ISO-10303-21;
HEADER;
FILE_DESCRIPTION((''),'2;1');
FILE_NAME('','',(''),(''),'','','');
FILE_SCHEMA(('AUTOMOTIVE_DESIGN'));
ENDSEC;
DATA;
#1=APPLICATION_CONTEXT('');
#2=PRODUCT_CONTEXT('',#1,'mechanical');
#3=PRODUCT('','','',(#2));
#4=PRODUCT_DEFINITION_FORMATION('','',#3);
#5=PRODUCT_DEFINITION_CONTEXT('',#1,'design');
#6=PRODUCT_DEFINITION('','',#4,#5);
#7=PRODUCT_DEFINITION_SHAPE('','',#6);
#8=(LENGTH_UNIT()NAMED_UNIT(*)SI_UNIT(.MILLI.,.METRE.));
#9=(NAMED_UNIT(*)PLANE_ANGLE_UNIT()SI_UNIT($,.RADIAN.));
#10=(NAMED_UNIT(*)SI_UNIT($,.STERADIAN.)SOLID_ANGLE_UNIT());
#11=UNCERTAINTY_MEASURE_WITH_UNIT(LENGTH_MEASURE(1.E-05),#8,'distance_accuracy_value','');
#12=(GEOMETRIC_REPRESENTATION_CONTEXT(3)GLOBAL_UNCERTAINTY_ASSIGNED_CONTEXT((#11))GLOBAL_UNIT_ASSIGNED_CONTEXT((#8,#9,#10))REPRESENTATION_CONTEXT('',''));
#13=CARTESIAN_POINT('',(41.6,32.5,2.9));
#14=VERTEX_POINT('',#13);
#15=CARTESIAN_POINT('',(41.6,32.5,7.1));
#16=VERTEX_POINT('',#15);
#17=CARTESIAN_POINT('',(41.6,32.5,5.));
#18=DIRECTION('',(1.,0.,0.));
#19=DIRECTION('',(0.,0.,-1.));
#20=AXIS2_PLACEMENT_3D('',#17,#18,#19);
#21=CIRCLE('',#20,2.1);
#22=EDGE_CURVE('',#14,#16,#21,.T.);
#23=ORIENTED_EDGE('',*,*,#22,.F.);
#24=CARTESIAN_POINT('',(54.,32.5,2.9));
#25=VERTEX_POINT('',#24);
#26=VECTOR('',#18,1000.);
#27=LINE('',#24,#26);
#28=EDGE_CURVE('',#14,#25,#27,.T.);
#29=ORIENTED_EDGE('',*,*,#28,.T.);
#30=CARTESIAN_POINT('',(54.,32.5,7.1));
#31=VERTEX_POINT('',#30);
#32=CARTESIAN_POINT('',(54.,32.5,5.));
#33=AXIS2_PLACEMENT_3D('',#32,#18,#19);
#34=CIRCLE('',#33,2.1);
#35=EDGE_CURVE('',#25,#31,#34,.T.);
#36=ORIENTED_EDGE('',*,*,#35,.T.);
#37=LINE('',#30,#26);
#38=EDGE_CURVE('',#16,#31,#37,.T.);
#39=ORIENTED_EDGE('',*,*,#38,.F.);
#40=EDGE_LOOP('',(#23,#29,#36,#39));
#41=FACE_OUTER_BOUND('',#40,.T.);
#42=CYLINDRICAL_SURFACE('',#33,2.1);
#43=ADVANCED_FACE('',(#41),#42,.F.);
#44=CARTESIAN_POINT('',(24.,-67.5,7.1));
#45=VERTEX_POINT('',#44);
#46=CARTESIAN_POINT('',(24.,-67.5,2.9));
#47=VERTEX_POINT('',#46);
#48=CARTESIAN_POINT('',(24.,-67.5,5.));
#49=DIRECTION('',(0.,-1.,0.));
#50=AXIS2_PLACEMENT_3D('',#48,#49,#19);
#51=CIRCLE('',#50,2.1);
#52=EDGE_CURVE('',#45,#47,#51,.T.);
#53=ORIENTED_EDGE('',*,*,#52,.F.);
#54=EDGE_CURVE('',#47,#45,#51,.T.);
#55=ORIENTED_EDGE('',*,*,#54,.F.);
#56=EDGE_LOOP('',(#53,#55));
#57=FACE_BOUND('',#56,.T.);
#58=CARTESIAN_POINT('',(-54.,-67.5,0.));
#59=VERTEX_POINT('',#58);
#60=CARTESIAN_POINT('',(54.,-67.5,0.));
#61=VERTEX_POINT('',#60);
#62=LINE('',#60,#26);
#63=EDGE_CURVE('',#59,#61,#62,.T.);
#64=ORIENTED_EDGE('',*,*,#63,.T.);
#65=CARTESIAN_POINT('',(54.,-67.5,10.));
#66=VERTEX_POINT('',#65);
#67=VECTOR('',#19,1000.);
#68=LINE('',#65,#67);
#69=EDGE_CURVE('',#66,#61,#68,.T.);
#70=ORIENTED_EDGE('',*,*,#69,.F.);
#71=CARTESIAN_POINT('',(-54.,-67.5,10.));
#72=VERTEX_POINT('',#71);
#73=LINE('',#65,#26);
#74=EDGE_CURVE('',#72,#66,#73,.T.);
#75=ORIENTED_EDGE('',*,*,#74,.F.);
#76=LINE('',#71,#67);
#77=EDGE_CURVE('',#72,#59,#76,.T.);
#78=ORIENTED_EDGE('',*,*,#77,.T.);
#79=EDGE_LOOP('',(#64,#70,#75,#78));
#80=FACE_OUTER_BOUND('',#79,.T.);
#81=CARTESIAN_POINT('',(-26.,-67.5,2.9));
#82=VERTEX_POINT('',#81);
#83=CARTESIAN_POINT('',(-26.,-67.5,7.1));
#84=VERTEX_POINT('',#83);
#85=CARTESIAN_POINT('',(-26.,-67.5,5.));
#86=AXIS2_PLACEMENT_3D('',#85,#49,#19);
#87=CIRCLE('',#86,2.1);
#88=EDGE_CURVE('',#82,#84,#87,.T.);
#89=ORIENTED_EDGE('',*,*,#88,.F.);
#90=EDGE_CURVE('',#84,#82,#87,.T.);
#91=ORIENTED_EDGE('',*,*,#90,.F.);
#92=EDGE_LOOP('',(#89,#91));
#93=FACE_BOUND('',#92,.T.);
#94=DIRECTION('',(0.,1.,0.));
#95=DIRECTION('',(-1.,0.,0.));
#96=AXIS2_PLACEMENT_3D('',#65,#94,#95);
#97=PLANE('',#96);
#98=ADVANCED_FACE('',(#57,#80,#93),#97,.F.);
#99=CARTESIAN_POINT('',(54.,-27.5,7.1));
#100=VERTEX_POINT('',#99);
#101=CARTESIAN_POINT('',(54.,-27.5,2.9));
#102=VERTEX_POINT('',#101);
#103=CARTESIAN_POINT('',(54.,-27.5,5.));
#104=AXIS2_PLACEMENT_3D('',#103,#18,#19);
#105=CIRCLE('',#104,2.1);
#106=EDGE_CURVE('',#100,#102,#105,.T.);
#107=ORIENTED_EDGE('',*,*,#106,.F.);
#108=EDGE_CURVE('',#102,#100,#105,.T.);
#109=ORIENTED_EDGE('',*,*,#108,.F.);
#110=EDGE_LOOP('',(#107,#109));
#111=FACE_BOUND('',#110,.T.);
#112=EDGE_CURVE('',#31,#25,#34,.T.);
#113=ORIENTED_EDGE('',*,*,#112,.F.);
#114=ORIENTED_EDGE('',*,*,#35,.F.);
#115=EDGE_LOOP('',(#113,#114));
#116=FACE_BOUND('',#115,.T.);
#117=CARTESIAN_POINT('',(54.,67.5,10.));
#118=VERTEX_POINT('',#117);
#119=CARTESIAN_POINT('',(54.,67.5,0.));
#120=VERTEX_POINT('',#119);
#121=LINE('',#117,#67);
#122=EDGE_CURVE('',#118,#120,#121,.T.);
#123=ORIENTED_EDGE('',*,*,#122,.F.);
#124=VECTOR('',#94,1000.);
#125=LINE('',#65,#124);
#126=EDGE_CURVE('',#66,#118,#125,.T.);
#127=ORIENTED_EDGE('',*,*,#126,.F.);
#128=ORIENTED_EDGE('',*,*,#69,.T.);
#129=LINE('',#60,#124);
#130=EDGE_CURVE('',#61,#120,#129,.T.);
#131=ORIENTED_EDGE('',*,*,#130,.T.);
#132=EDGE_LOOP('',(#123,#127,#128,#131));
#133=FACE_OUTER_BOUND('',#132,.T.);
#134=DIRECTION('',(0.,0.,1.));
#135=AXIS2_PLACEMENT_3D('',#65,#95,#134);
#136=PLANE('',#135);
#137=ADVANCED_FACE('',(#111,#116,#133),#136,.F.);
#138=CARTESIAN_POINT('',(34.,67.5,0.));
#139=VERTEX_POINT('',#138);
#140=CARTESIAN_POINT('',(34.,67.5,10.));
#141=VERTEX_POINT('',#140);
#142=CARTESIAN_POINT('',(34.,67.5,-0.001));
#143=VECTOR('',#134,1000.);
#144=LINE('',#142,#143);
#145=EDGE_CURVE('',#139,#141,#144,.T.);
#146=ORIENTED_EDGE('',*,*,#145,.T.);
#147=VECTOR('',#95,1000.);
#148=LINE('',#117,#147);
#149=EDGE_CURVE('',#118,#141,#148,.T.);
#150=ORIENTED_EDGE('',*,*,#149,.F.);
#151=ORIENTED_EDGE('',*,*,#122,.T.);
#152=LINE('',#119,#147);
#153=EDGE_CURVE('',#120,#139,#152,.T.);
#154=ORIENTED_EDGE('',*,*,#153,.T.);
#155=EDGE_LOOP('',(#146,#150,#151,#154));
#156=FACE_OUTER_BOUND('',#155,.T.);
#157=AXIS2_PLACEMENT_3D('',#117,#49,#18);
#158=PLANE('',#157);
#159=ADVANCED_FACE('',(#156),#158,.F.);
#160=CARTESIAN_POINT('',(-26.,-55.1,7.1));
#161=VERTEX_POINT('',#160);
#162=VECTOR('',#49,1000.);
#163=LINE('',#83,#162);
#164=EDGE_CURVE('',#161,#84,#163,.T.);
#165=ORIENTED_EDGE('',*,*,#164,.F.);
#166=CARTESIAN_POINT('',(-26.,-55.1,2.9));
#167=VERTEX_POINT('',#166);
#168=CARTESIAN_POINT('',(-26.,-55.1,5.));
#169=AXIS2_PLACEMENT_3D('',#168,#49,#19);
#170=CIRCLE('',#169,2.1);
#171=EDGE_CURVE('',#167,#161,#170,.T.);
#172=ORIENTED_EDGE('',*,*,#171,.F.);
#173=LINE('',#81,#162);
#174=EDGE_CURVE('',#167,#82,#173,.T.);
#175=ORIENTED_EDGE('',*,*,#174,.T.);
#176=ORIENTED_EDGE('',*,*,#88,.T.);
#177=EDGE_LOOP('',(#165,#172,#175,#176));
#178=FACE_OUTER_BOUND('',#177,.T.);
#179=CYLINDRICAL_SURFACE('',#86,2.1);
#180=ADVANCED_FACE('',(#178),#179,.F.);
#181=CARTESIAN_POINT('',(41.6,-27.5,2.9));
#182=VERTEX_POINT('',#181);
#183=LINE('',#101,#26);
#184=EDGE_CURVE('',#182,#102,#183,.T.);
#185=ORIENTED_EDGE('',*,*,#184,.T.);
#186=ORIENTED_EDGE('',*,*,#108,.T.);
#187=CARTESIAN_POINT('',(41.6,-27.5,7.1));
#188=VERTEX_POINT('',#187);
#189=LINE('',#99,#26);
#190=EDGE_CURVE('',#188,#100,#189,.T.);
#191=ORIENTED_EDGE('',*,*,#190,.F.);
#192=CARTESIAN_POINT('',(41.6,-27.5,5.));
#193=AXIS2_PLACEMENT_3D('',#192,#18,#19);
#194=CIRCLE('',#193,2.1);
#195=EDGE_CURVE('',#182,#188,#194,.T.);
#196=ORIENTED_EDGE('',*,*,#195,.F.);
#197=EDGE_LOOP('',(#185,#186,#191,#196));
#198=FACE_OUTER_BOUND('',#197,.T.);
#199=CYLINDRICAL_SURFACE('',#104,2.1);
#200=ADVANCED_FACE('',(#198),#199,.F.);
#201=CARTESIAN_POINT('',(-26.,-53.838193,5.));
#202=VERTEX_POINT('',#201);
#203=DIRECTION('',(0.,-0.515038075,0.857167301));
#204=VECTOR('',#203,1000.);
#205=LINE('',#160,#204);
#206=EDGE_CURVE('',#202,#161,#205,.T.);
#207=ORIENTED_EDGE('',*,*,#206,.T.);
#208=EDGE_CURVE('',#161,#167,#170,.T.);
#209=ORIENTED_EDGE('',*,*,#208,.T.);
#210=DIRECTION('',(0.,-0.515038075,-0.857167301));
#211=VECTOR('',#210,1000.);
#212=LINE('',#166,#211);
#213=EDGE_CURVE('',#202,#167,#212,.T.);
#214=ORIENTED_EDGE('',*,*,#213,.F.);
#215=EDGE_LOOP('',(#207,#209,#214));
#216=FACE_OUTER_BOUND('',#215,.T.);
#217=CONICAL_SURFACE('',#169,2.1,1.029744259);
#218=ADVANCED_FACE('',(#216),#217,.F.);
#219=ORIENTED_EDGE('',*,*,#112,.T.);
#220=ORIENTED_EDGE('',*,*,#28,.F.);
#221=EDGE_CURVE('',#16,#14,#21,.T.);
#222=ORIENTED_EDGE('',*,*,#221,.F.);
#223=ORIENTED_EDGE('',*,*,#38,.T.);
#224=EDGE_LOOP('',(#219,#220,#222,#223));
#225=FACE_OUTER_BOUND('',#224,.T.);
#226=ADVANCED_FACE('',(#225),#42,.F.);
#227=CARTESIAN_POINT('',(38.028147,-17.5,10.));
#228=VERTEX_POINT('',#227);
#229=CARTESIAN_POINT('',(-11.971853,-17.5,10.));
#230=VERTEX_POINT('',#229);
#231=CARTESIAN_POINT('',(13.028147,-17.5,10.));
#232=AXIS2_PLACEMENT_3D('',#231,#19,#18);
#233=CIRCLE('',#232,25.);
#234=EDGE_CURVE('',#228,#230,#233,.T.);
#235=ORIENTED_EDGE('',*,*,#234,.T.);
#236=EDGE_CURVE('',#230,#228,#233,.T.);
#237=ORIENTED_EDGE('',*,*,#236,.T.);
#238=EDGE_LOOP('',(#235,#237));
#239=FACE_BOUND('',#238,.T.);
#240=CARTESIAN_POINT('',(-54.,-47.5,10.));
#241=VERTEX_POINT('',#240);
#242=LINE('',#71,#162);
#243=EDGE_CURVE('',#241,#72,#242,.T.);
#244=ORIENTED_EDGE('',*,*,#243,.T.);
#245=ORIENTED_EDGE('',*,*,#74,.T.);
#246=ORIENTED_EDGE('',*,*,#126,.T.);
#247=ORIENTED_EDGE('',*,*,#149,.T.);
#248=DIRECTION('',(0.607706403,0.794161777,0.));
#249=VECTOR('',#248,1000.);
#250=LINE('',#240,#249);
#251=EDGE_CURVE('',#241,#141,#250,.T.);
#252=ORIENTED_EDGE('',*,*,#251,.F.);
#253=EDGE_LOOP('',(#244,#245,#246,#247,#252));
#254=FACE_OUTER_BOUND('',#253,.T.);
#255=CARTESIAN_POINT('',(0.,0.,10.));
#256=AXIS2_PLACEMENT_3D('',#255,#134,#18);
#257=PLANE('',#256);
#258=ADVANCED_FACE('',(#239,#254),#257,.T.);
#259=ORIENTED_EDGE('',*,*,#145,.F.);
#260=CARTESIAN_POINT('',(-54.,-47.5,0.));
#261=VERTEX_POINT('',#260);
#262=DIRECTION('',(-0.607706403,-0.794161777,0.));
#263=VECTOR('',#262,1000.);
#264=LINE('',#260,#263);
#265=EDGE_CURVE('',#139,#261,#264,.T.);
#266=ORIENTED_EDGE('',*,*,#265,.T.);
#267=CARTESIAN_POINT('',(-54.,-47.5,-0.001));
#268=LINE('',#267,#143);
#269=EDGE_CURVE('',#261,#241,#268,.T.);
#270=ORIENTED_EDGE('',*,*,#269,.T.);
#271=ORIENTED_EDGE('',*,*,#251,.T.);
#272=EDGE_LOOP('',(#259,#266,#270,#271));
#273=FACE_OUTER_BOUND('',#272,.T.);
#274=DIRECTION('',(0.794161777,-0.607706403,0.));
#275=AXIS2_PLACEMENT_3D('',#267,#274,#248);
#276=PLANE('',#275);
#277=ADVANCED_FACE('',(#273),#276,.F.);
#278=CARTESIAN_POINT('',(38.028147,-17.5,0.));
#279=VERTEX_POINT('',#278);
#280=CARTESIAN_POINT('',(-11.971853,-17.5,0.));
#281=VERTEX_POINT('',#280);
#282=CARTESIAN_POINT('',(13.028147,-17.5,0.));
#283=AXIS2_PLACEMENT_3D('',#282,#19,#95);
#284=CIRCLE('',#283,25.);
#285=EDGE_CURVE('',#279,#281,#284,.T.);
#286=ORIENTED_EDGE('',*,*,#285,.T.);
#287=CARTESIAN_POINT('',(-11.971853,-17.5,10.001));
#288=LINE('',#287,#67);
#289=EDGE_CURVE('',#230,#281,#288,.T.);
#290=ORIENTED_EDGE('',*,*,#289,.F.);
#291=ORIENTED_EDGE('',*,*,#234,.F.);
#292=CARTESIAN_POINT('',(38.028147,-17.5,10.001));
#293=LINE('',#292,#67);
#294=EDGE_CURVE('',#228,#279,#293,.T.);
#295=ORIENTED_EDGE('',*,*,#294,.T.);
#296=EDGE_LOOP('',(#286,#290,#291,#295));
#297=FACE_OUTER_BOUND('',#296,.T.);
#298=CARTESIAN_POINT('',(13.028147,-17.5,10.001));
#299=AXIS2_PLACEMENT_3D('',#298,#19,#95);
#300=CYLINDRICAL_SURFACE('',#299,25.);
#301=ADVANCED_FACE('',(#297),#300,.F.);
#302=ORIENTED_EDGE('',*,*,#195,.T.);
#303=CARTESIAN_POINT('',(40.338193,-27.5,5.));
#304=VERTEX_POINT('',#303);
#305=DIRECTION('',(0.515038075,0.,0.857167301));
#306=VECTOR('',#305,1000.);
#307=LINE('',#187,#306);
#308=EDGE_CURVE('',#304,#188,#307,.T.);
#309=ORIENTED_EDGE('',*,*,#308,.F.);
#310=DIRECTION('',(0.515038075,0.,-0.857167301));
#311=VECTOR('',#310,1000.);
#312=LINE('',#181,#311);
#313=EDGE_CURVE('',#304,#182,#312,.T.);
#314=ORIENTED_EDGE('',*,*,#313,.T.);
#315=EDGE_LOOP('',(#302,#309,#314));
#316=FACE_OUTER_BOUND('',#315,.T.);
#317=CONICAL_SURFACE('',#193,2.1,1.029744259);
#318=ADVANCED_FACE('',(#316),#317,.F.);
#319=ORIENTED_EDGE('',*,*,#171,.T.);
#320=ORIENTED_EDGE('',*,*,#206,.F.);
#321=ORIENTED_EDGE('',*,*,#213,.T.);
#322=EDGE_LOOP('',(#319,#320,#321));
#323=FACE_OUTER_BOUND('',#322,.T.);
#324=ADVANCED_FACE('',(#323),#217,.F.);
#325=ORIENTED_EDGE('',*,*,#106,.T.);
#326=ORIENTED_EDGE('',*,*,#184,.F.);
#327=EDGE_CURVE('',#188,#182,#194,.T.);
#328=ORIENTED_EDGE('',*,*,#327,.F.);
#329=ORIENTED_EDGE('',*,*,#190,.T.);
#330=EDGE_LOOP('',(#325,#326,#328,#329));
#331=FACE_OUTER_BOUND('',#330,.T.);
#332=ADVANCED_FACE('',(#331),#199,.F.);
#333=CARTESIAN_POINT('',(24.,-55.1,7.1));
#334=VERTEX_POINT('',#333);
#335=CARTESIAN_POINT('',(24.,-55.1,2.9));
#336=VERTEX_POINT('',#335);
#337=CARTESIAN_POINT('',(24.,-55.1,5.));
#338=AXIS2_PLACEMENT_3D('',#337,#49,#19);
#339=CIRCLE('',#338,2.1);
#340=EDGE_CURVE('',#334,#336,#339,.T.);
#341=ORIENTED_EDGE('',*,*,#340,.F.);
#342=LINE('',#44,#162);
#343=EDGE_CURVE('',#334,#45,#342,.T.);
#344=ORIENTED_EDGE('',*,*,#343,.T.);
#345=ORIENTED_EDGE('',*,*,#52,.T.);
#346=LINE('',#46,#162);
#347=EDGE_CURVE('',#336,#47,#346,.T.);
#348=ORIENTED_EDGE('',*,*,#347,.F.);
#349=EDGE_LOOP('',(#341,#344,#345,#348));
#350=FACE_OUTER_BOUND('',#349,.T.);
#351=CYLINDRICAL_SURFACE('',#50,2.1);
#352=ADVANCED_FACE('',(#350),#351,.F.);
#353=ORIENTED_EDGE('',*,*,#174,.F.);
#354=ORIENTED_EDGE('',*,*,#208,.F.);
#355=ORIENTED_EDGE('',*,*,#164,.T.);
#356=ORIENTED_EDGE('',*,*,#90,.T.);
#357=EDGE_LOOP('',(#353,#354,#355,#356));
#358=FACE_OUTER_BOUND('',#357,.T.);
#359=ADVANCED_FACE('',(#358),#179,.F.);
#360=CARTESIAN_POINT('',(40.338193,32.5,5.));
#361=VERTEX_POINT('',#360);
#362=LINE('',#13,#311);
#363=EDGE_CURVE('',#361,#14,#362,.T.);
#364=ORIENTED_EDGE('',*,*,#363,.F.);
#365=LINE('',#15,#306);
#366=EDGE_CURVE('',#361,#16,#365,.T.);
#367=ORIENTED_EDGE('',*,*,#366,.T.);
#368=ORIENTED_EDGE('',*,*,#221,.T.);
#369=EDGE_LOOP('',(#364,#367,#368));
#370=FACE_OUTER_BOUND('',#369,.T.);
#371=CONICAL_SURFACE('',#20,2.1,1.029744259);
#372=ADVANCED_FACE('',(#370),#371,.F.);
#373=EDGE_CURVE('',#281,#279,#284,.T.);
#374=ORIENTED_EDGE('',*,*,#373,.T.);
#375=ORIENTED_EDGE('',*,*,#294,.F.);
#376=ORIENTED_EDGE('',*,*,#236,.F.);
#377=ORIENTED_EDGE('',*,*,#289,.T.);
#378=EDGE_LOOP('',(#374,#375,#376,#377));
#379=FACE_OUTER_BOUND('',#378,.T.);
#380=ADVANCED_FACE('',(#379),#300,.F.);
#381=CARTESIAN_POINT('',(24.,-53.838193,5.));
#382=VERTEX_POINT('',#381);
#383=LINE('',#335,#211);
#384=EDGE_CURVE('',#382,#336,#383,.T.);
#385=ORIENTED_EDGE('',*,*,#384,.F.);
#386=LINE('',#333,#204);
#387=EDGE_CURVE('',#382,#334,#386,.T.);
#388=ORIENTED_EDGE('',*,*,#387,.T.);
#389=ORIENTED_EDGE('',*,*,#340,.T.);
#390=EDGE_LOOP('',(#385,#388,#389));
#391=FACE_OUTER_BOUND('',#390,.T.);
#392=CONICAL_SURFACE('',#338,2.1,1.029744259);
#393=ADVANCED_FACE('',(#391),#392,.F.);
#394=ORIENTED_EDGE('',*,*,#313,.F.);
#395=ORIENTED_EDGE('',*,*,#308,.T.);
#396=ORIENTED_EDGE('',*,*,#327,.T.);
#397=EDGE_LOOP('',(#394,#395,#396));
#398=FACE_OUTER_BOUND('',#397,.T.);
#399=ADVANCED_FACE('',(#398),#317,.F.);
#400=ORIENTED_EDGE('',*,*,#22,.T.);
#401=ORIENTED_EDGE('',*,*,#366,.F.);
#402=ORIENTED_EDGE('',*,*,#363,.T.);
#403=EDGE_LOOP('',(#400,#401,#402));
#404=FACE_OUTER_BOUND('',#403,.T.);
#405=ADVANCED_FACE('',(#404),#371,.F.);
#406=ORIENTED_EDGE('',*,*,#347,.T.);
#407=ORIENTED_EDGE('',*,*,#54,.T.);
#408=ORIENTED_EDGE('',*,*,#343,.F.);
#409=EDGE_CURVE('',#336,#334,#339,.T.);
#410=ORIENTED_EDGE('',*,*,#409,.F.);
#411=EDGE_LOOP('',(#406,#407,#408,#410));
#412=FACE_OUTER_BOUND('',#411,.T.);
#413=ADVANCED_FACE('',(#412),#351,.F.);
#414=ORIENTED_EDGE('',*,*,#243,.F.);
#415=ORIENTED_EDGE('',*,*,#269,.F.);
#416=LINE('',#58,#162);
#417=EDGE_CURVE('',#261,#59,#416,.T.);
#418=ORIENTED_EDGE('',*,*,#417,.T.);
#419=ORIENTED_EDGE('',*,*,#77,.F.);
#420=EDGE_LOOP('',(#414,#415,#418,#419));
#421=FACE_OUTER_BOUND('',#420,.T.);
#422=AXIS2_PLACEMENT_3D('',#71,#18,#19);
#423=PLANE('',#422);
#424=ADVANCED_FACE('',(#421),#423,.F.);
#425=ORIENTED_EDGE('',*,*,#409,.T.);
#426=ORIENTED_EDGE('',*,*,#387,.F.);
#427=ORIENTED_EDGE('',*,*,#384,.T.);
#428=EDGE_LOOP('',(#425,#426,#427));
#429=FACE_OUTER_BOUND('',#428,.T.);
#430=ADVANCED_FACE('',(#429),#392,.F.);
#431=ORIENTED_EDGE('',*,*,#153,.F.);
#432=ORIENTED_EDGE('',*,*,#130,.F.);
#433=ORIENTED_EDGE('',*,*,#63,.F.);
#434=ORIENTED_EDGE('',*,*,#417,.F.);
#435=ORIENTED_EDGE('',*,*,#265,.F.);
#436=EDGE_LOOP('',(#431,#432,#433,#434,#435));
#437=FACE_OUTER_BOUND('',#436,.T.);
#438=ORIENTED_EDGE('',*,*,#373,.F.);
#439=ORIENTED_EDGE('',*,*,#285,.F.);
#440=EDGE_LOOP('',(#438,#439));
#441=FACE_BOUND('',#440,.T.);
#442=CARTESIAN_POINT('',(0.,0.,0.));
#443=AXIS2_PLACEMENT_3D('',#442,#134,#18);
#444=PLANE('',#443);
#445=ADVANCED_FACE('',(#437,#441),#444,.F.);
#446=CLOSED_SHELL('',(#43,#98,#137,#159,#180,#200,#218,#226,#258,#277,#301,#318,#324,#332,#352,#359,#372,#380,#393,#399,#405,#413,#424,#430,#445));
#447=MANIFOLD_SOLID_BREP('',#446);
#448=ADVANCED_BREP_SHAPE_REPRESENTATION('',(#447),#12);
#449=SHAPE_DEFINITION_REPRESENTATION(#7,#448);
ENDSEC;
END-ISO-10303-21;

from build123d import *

# Parameters (mm, degrees)
SKETCH_1_W             = 108
SKETCH_1_H             = 135
EXTRUDE_1_DEPTH        = 10
CUT_EXTRUDE_1_REACH    = 89.019
HOLE_WIZARD_M5_1_D     = 4.2
HOLE_WIZARD_M5_1_DEPTH = 12.4
HOLE_WIZARD_M5_1_TIP   = 1.2618073
HOLE_WIZARD_M5_2_D     = 4.2
HOLE_WIZARD_M5_2_DEPTH = 12.4
HOLE_WIZARD_M5_2_TIP   = 1.2618073
CUT_EXTRUDE_2_REACH    = 89.019
SKETCH_7_R             = 25


with BuildPart() as part:
    # 草图1 → 凸台-拉伸1 (new body)
    with BuildSketch(Plane.XY):
        Rectangle(SKETCH_1_W, SKETCH_1_H)
    extrude(amount=EXTRUDE_1_DEPTH)

    # 草图2 → 切除-拉伸1 (cut, up to next)
    with BuildSketch(Plane.XY.offset(10), mode=Mode.PRIVATE) as cut_extrude_1_sk1:
        Polygon((34, 67.5), (-54, 67.5), (-54, -47.5), align=None)
    cut_extrude_1_tool1 = extrude(cut_extrude_1_sk1.sketch, amount=-CUT_EXTRUDE_1_REACH, mode=Mode.PRIVATE) & part.part
    add(cut_extrude_1_tool1.solids().sort_by_distance((-24.666667, 29.166667, 10))[0], mode=Mode.SUBTRACT)

    # M5 螺纹孔1
    with Locations(Plane(origin=(0, -67.5, 0), x_dir=(-1, 0, 0), z_dir=(0, -1, 0))):
        with Locations((-24, -5), (26, -5)):
            Hole(HOLE_WIZARD_M5_1_D / 2, depth=HOLE_WIZARD_M5_1_DEPTH)
            with Locations((0, 0, -(HOLE_WIZARD_M5_1_DEPTH + HOLE_WIZARD_M5_1_TIP / 2))):  # 118° drill point
                Cone(0, HOLE_WIZARD_M5_1_D / 2, HOLE_WIZARD_M5_1_TIP, mode=Mode.SUBTRACT)

    # M5 螺纹孔2
    with Locations(Plane(origin=(54, 0, 0), x_dir=(0, 0, -1), z_dir=(1, 0, 0))):
        with Locations((-5, -27.5), (-5, 32.5)):
            Hole(HOLE_WIZARD_M5_2_D / 2, depth=HOLE_WIZARD_M5_2_DEPTH)
            with Locations((0, 0, -(HOLE_WIZARD_M5_2_DEPTH + HOLE_WIZARD_M5_2_TIP / 2))):  # 118° drill point
                Cone(0, HOLE_WIZARD_M5_2_D / 2, HOLE_WIZARD_M5_2_TIP, mode=Mode.SUBTRACT)

    # 草图7 → 切除-拉伸2 (cut, up to next)
    with BuildSketch(Plane(origin=(0, 0, 0), x_dir=(-1, 0, 0), z_dir=(0, 0, -1)), mode=Mode.PRIVATE) as cut_extrude_2_sk1:
        with Locations((-13.028146721, -17.5)):
            Circle(SKETCH_7_R)
    cut_extrude_2_tool1 = extrude(cut_extrude_2_sk1.sketch, amount=-CUT_EXTRUDE_2_REACH, mode=Mode.PRIVATE) & part.part
    add(cut_extrude_2_tool1.solids().sort_by_distance((13.028147, -17.5, 0))[0], mode=Mode.SUBTRACT)


solid = part.part
